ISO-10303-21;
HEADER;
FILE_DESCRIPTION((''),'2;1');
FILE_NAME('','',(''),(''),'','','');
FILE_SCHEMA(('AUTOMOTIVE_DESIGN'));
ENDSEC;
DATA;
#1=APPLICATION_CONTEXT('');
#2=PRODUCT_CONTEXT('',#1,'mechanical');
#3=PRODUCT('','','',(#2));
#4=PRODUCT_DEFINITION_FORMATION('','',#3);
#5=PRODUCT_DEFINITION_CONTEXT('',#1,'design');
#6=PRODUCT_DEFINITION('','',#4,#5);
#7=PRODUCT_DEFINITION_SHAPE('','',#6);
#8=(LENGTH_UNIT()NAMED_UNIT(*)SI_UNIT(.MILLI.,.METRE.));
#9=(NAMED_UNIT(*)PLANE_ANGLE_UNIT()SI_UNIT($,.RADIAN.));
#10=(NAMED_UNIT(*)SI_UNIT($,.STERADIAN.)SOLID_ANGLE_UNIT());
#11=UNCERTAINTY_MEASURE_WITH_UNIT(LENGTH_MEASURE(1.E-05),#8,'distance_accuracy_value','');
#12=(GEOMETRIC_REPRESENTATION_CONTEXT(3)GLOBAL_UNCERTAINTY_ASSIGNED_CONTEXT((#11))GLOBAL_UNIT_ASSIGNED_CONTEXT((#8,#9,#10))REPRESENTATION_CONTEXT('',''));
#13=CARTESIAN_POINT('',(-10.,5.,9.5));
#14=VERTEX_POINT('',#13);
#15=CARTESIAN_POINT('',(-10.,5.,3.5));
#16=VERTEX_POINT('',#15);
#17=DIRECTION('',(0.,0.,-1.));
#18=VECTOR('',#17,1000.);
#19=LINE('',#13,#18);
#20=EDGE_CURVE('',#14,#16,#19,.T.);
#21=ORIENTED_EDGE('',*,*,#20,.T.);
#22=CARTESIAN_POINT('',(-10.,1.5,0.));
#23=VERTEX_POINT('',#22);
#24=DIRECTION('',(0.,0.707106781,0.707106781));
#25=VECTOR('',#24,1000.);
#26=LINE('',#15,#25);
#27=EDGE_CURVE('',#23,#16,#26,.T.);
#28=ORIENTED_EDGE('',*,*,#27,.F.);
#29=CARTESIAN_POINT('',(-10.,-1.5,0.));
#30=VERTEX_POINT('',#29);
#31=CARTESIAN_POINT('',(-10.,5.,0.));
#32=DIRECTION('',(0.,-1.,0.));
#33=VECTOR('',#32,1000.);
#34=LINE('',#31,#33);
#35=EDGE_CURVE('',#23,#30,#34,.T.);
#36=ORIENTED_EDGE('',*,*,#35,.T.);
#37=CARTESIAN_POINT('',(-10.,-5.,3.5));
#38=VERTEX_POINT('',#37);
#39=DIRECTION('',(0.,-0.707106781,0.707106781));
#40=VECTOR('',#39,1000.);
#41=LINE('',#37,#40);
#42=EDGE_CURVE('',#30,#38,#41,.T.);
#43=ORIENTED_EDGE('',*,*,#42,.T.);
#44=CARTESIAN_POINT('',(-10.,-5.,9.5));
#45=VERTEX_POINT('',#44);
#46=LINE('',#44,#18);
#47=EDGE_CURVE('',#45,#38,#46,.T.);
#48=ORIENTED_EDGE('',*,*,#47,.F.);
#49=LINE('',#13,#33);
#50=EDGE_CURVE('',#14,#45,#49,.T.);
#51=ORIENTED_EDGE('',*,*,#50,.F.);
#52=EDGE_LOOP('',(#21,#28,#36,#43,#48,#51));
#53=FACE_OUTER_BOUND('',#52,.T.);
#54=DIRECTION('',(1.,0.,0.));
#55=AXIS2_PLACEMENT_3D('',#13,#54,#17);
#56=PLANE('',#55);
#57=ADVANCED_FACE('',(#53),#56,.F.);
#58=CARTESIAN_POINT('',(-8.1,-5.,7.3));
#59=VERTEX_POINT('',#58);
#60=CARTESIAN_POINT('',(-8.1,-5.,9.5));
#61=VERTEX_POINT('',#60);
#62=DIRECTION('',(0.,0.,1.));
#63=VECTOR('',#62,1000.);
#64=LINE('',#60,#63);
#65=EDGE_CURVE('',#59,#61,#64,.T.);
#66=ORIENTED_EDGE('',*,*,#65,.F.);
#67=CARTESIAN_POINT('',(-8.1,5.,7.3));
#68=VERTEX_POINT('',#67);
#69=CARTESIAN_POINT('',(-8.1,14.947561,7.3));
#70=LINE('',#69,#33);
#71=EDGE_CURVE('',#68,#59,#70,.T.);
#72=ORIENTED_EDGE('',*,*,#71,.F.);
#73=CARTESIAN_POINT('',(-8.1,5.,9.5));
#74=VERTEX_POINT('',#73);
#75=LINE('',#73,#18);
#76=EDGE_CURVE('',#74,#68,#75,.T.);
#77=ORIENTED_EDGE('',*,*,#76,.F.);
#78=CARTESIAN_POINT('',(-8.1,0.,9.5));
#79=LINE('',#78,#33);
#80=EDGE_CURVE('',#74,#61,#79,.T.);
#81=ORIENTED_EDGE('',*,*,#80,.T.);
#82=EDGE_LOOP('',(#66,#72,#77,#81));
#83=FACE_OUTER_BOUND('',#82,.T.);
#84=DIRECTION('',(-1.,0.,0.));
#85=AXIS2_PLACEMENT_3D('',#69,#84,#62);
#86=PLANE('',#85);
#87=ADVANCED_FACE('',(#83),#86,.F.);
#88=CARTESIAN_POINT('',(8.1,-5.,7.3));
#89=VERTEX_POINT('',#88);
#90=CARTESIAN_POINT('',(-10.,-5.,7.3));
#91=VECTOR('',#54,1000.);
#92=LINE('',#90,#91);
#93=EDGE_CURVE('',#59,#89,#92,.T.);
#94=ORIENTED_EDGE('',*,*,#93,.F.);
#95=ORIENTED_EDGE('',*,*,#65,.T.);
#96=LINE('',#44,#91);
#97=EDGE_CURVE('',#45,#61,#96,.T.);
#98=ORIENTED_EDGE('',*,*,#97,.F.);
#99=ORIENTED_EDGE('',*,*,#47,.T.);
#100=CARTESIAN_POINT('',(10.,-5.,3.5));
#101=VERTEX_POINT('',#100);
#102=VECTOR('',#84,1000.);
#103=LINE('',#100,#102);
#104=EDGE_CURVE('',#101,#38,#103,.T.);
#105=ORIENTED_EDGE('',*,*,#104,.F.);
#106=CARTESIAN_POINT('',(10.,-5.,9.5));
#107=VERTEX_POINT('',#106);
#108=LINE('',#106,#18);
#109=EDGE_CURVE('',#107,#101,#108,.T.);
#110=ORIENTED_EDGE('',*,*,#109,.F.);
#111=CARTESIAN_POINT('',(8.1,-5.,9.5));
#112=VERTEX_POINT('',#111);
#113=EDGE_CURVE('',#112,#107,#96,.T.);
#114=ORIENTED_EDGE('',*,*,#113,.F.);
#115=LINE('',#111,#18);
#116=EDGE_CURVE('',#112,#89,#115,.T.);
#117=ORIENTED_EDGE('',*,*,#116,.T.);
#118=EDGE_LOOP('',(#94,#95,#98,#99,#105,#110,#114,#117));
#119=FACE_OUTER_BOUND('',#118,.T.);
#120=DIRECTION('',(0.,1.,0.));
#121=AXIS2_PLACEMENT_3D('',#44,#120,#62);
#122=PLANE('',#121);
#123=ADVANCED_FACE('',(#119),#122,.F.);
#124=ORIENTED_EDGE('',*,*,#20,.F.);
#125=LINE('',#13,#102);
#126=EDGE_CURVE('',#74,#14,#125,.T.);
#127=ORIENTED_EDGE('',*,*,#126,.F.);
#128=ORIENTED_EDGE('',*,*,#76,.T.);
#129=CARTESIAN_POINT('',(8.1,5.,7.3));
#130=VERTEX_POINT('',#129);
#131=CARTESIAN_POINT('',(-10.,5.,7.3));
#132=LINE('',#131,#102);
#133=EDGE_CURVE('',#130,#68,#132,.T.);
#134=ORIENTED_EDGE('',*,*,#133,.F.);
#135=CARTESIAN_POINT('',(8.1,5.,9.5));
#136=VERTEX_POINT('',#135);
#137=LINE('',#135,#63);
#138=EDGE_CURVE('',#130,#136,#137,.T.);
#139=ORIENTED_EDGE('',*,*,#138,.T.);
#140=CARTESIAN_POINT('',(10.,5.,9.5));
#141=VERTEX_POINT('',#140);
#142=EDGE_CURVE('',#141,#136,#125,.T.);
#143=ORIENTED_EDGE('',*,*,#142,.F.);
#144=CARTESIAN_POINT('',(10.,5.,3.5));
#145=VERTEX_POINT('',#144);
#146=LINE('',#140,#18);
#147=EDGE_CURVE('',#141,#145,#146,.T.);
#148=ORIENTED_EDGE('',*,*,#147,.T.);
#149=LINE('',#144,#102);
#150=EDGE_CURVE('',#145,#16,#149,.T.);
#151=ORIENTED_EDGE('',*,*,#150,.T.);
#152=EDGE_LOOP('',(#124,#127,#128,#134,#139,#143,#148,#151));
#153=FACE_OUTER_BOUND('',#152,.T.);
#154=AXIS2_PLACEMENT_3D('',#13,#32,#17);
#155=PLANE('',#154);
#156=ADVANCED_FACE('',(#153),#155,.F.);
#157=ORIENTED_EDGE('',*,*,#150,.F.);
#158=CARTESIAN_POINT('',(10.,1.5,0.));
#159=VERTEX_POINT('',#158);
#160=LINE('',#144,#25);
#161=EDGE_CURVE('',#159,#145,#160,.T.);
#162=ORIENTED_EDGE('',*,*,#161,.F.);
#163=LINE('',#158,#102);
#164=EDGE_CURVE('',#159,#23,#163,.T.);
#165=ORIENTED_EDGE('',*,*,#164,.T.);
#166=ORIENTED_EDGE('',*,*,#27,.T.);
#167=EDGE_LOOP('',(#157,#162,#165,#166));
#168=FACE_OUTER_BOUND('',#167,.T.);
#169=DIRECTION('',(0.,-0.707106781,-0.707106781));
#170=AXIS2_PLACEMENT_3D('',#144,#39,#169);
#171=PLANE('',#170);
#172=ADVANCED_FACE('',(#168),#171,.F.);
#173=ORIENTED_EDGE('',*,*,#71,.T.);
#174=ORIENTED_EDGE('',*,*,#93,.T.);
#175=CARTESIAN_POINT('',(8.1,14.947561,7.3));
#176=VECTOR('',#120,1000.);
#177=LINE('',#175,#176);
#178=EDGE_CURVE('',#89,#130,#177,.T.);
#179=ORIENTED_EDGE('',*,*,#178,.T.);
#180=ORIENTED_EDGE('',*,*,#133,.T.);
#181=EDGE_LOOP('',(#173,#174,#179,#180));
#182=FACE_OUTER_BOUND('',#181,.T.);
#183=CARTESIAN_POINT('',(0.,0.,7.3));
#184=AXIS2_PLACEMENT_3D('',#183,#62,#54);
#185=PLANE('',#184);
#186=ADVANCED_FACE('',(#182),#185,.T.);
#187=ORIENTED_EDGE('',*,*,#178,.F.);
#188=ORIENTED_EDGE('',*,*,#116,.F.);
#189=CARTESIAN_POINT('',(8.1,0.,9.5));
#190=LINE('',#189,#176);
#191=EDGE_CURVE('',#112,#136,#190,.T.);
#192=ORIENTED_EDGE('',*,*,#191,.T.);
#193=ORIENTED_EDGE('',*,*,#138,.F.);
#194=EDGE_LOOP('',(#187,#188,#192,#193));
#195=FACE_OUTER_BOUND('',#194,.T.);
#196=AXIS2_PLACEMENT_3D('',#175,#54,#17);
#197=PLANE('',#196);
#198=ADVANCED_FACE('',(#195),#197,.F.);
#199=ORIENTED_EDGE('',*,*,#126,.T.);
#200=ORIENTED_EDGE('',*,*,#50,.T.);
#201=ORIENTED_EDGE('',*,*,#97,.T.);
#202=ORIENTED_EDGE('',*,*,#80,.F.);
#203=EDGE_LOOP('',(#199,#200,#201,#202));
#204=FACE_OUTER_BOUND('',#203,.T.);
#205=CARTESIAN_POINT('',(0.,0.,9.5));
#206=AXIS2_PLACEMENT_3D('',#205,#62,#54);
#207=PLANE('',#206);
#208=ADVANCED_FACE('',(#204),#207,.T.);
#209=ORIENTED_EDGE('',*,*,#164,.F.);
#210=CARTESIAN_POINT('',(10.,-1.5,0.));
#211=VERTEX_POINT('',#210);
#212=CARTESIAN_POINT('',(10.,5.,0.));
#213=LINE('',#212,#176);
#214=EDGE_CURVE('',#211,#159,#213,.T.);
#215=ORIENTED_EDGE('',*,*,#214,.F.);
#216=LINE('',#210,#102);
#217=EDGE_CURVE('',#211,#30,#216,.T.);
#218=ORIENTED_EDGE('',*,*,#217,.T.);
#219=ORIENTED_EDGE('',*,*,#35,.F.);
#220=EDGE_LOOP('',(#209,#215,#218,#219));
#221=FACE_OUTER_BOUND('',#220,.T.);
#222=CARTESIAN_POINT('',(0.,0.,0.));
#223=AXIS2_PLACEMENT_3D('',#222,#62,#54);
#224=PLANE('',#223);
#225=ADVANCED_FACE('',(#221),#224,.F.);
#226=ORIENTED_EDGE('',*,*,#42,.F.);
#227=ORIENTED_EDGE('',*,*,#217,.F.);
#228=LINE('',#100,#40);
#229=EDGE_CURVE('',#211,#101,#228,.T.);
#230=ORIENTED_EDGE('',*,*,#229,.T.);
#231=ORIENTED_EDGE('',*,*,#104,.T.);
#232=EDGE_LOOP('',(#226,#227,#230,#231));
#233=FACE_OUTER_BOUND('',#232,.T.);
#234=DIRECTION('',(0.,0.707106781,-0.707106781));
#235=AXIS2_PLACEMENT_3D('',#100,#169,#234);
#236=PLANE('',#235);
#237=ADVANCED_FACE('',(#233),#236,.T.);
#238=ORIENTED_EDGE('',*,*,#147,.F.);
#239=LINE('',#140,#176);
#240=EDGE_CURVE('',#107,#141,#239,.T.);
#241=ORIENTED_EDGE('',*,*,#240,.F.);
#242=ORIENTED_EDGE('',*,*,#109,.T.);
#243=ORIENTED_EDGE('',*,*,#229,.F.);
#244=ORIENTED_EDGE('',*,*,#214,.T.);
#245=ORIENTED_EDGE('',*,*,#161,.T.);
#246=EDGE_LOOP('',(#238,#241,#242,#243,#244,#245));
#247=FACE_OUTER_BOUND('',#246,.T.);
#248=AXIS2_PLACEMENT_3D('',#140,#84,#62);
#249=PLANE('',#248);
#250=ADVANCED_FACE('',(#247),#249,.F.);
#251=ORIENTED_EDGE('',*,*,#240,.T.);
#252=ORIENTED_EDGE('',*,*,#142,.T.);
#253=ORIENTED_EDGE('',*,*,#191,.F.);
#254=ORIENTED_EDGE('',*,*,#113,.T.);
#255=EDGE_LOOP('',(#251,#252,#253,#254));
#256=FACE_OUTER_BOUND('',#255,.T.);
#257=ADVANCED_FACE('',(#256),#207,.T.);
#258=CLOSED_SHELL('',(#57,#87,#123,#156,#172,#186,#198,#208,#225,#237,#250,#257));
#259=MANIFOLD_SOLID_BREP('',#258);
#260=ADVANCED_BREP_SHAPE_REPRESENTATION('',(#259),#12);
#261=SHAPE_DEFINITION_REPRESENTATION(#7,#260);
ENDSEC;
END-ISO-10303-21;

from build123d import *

# Parameters (mm, degrees)
SKETCH_1_W          = 20
SKETCH_1_H          = 10
EXTRUDE_1_DEPTH     = 9.5
SKETCH_2_W          = 16.2
SKETCH_2_H          = 29.89512134
CUT_EXTRUDE_1_DEPTH = 2.2
CUT_EXTRUDE_2_DEPTH = 23.699118926


with BuildPart() as part:
    # 草图1 → 凸台-拉伸1 (new body)
    with BuildSketch(Plane.XY):
        Rectangle(SKETCH_1_W, SKETCH_1_H)
    extrude(amount=EXTRUDE_1_DEPTH)

    # 草图2 → 切除-拉伸1 (cut)
    with BuildSketch(Plane.XY.offset(9.5)):
        Rectangle(SKETCH_2_W, SKETCH_2_H)
    extrude(amount=-CUT_EXTRUDE_1_DEPTH, mode=Mode.SUBTRACT)

    # 草图3 → 切除-拉伸2 (cut, through all)
    with BuildSketch(Plane.ZY.offset(10)):
        Polygon((0, 5), (3.5, 5), (0, 1.5), align=None)
    cut_extrude_2 = extrude(amount=-CUT_EXTRUDE_2_DEPTH, mode=Mode.SUBTRACT)

    # 镜向1: 切除-拉伸2 across plane
    add(cut_extrude_2.mirror(Plane.ZX), mode=Mode.SUBTRACT)


solid = part.part
